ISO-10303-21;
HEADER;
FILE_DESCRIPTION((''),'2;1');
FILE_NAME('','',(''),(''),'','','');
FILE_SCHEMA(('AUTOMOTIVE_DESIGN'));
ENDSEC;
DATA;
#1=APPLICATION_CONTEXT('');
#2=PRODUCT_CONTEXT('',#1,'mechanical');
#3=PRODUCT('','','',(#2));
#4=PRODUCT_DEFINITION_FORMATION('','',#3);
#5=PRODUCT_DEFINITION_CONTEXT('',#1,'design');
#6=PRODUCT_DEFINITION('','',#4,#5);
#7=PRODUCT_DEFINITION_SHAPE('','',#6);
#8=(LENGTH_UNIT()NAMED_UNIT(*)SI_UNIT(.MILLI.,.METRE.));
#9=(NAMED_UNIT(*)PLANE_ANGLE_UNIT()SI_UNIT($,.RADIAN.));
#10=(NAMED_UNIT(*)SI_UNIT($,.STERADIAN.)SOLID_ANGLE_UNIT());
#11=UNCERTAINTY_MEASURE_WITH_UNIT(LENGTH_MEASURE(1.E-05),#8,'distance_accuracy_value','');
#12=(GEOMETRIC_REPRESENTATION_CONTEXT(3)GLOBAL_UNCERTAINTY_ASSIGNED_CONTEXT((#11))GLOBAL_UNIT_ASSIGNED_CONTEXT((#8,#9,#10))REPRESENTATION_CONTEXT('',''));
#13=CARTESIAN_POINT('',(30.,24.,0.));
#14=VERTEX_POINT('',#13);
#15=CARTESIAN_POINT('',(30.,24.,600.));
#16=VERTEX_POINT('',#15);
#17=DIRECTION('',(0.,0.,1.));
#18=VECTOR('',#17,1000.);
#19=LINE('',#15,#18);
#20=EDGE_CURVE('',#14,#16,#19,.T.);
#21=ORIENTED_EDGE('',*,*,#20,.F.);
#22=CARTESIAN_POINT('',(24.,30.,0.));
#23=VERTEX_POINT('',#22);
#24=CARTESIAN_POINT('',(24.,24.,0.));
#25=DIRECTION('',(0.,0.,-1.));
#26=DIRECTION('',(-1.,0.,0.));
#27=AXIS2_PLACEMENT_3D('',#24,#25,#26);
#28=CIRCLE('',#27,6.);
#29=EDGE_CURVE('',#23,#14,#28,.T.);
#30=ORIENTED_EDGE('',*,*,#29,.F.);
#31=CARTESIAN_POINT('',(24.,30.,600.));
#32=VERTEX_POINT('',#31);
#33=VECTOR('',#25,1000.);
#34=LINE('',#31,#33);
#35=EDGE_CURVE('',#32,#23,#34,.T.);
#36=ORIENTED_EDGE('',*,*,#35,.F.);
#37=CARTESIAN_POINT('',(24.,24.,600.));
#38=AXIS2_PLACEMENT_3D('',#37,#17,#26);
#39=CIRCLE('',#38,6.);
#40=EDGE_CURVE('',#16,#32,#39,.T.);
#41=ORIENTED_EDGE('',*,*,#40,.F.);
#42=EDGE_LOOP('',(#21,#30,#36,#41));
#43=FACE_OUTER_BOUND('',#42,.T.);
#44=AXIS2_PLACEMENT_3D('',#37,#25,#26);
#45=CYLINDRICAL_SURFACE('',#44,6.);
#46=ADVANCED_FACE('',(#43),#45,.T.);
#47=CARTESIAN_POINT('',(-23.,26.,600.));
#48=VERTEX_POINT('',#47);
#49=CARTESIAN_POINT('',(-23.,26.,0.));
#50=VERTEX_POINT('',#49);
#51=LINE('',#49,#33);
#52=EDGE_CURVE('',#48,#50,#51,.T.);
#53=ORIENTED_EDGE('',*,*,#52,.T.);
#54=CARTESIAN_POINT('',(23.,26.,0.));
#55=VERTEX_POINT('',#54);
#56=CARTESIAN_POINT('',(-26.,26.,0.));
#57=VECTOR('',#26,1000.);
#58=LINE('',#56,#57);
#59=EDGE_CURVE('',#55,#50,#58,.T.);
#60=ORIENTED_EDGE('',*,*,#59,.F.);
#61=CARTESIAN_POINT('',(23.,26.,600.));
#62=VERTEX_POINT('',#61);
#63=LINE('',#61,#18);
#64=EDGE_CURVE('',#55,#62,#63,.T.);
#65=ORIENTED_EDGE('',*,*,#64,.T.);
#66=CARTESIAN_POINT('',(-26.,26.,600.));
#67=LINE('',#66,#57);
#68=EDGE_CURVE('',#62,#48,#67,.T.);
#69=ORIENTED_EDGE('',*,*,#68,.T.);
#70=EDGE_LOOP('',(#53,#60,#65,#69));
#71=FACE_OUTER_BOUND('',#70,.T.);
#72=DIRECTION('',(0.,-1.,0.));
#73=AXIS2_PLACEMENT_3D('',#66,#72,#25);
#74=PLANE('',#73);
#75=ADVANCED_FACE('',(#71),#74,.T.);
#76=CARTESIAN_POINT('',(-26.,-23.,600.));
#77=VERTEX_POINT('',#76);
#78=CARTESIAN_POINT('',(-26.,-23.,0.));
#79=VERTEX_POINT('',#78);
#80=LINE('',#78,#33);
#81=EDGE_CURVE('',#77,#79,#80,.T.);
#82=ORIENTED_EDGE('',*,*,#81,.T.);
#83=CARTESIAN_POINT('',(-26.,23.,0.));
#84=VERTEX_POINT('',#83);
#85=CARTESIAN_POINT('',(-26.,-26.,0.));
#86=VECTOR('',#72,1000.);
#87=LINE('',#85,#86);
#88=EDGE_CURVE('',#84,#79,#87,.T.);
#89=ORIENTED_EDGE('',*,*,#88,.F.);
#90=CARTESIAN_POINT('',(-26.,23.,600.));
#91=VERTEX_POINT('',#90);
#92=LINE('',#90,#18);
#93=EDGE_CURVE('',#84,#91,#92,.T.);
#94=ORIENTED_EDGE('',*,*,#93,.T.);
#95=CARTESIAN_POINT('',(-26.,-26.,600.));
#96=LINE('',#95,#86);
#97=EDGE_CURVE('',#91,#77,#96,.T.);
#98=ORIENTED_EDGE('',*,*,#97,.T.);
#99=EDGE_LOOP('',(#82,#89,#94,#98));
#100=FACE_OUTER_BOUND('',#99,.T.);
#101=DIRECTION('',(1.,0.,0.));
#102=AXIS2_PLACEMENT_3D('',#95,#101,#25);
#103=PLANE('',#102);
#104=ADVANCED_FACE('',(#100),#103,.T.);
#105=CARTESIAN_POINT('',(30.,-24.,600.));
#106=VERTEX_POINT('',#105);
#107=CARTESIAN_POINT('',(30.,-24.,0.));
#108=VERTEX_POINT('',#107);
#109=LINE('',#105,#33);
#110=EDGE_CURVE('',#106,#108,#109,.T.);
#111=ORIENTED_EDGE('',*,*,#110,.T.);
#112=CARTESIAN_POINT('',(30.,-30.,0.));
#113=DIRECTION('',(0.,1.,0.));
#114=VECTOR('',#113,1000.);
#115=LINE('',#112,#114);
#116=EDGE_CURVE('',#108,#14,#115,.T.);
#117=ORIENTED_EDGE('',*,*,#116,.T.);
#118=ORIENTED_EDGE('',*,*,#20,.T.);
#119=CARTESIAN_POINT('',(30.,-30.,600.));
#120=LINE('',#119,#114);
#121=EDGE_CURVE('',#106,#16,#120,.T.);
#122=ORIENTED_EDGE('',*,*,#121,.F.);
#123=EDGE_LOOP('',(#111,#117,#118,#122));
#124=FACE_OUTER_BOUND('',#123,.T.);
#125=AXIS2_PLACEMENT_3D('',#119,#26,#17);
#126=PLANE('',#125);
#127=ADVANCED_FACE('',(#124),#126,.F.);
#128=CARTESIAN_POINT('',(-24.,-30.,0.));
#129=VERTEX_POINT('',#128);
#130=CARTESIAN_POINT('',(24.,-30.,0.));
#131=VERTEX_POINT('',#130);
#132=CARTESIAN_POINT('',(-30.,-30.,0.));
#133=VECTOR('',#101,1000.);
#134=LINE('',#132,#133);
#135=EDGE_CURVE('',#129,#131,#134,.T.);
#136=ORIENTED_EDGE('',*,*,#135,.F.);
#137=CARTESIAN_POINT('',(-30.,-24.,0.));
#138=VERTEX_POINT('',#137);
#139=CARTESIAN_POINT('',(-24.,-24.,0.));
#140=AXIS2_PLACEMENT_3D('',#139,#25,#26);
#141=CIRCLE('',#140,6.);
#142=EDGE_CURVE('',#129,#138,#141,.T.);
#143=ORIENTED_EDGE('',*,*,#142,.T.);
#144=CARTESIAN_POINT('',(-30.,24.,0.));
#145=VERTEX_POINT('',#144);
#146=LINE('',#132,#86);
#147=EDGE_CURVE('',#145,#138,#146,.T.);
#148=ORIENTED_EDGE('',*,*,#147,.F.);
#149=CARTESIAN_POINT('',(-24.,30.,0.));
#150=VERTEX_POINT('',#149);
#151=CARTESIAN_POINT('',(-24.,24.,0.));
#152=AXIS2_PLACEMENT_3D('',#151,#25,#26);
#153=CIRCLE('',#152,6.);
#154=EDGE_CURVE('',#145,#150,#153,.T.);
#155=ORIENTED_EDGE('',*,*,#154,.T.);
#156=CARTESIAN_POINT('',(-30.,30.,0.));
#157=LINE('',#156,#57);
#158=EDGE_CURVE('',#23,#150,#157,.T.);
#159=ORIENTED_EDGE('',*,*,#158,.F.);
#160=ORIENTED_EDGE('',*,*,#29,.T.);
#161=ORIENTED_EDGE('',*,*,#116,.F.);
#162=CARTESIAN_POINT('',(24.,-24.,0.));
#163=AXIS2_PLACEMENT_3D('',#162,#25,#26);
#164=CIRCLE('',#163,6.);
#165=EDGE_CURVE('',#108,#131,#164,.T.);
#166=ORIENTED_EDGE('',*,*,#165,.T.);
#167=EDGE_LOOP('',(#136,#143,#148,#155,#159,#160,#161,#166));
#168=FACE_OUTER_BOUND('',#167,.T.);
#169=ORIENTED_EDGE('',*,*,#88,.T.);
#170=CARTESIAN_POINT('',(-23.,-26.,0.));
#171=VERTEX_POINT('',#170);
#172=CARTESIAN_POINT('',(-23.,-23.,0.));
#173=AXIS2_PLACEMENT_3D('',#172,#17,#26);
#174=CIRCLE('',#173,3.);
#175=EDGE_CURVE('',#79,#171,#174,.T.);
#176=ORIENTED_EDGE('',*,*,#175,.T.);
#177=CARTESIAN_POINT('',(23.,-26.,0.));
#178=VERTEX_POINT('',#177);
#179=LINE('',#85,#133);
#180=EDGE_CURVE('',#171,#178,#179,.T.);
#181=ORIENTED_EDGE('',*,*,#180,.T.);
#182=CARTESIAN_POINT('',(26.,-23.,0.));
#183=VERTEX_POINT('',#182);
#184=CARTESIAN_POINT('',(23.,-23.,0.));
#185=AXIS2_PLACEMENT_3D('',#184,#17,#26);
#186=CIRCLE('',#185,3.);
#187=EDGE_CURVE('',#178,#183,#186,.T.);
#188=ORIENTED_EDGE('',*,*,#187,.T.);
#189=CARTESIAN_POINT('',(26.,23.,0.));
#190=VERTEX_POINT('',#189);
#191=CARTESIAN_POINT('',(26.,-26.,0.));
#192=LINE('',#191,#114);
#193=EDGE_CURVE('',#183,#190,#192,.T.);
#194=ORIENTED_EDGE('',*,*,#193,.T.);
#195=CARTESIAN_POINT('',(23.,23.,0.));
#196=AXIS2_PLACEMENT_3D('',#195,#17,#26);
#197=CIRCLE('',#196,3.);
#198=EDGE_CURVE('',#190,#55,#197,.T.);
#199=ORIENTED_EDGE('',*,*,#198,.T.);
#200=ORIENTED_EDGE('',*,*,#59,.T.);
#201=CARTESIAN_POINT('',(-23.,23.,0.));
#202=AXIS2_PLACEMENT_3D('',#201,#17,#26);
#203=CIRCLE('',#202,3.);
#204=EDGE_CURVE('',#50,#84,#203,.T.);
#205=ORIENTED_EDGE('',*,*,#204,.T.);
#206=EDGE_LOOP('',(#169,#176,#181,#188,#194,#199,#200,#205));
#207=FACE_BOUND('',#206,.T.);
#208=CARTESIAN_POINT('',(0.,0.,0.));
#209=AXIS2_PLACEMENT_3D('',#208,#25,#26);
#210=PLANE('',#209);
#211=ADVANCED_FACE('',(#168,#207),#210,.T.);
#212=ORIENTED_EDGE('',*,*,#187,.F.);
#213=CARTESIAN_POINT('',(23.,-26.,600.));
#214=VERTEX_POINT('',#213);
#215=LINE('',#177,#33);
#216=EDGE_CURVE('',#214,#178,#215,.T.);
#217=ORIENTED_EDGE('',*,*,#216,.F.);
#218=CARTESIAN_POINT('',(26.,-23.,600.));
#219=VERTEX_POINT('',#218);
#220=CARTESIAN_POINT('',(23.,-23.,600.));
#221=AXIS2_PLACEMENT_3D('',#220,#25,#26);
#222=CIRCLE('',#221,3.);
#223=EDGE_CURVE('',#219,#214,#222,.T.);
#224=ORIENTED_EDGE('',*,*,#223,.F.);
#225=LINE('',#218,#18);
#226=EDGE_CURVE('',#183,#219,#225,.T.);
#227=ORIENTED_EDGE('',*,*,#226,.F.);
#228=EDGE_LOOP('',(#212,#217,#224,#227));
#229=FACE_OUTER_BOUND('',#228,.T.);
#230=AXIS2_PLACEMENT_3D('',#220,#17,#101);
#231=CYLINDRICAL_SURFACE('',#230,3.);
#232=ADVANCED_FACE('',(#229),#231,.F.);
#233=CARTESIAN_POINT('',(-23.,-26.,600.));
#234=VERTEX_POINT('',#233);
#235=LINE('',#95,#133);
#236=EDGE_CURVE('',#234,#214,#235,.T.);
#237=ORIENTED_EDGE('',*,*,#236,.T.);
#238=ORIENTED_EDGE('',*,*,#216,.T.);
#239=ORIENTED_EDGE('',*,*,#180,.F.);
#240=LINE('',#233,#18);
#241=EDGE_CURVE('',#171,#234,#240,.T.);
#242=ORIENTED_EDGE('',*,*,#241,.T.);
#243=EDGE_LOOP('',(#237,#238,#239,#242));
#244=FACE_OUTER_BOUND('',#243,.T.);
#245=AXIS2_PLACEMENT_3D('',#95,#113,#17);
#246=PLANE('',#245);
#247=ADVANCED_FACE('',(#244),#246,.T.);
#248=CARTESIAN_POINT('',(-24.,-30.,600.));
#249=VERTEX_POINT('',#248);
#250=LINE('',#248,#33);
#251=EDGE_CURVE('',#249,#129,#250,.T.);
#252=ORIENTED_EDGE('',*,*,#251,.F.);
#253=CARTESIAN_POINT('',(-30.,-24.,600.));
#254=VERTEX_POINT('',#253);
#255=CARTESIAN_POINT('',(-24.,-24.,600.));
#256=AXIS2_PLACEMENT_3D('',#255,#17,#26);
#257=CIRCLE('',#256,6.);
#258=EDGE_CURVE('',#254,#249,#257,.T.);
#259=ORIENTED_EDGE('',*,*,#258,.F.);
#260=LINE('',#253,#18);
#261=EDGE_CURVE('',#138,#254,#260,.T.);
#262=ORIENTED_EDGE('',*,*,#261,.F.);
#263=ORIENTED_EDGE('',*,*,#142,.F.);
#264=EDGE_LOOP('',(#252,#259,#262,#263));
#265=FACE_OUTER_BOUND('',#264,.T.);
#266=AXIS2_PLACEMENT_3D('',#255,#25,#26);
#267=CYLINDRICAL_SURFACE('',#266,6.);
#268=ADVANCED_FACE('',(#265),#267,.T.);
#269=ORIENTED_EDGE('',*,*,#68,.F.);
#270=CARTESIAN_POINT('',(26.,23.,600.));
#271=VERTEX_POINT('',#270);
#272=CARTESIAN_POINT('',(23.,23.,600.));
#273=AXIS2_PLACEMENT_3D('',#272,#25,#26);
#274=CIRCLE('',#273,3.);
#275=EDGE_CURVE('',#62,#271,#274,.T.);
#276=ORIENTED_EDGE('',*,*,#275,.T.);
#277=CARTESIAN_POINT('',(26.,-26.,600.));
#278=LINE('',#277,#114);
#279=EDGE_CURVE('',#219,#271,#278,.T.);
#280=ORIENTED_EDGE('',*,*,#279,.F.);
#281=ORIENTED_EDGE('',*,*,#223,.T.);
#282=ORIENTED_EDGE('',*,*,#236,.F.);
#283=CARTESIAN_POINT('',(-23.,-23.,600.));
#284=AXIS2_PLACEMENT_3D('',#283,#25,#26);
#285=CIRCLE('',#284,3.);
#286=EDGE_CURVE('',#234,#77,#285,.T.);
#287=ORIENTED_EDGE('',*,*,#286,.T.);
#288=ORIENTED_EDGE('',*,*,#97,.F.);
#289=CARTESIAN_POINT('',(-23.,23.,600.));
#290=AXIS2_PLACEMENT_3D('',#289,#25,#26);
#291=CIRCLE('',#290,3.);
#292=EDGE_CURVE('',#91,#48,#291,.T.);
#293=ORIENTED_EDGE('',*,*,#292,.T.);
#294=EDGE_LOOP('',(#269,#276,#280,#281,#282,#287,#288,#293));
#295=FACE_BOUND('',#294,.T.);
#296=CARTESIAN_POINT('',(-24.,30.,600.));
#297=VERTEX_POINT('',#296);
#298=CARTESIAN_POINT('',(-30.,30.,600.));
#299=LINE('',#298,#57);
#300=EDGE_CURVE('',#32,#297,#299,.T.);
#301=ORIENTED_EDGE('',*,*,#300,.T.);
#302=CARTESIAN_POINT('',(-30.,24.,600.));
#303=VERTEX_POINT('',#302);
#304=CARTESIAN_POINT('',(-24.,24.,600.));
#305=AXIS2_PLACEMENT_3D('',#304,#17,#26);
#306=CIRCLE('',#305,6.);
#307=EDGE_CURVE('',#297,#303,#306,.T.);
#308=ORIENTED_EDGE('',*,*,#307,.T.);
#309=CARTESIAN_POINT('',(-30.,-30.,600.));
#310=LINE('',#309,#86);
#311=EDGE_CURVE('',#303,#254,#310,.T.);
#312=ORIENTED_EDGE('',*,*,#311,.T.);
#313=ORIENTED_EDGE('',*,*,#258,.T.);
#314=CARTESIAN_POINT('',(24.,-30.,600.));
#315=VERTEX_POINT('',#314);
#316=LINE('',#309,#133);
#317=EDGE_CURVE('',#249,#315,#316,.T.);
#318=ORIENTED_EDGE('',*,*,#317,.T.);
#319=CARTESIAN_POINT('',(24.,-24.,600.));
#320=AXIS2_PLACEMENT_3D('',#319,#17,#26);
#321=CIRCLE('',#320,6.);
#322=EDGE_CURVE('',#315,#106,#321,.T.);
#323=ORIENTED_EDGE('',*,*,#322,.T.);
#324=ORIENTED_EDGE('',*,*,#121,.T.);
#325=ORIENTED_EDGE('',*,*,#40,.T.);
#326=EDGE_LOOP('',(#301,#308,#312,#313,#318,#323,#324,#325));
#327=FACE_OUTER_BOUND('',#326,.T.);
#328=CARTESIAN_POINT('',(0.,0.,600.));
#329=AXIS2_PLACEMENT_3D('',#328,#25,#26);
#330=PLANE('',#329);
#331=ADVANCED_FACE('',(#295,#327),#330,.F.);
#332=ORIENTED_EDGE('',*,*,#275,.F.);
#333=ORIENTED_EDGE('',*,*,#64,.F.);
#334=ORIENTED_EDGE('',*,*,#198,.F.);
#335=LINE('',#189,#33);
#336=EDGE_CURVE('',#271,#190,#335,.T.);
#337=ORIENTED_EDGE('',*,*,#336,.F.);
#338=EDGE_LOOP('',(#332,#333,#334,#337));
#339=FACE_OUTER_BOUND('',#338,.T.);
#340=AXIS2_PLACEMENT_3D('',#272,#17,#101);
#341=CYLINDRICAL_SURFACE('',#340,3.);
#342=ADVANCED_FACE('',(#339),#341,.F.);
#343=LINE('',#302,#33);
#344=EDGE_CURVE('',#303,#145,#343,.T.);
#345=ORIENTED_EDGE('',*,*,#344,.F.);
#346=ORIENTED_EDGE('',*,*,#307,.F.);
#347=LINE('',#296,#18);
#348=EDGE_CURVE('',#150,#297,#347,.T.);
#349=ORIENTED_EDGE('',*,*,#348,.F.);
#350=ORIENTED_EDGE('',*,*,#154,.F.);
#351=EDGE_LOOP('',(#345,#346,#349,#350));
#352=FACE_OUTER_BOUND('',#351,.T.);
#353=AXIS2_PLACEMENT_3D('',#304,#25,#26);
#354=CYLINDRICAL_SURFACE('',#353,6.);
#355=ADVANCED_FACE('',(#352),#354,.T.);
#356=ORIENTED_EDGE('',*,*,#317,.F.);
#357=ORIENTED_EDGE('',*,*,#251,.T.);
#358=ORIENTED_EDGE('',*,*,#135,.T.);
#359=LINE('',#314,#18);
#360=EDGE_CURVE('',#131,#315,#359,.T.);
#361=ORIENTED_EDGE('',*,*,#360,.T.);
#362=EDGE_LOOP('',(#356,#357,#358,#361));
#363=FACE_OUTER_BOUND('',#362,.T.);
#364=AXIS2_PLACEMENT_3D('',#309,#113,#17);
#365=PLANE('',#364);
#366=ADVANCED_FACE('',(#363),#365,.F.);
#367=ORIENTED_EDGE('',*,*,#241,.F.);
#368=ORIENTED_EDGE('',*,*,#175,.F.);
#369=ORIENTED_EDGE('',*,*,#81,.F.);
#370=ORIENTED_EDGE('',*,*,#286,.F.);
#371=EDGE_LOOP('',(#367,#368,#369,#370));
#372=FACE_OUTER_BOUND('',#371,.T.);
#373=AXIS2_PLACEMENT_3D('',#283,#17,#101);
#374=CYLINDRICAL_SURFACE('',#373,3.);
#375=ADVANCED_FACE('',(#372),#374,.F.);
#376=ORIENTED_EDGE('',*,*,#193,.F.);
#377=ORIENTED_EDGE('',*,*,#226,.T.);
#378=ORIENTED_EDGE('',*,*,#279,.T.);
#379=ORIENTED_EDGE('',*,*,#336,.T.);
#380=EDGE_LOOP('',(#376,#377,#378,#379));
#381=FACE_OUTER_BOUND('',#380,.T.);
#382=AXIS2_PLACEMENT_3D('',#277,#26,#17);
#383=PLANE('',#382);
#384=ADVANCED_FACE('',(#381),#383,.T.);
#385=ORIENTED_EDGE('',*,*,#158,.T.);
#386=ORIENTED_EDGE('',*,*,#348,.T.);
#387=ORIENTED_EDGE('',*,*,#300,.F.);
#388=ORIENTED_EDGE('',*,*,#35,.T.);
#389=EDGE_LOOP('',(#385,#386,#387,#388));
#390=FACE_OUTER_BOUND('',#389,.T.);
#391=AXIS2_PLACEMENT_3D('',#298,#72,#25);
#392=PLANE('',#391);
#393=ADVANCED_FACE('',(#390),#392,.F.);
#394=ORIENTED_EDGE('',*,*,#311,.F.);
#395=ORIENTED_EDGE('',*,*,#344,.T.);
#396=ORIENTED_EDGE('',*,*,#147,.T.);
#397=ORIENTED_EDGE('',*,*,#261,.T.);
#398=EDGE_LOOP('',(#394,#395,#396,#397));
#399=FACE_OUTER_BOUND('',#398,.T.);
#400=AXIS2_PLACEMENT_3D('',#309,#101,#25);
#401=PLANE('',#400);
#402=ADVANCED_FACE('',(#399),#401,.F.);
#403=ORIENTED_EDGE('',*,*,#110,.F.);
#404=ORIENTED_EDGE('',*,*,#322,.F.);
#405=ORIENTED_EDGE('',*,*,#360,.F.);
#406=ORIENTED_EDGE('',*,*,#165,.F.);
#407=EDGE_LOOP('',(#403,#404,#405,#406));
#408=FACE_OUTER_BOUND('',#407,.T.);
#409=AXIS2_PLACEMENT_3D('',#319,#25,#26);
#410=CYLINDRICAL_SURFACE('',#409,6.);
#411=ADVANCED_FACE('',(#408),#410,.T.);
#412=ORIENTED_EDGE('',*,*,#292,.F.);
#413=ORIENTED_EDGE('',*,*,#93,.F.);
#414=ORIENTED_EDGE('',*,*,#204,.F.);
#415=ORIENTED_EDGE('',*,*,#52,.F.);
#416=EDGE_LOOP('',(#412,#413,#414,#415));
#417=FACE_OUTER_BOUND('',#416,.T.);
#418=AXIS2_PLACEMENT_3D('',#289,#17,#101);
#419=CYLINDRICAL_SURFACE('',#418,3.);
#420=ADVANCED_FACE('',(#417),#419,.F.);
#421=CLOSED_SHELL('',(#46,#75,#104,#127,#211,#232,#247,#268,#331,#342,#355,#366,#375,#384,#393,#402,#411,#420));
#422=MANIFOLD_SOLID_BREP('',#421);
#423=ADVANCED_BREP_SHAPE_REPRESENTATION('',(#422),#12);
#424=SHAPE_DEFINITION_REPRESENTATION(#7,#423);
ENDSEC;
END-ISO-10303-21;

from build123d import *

# Parameters (mm, degrees)
SKETCH1_W           = 60
SKETCH1_H           = 60
SKETCH1_W_2         = 52
SKETCH1_H_2         = 52
BOSS_EXTRUDE1_DEPTH = 600
FILLET1_R           = 6
FILLET2_R           = 3


with BuildPart() as part:
    # Sketch1 → Boss-Extrude1 (new body)
    with BuildSketch(Plane.XY):
        Rectangle(SKETCH1_W, SKETCH1_H)
        Rectangle(SKETCH1_W_2, SKETCH1_H_2, mode=Mode.SUBTRACT)
    extrude(amount=BOSS_EXTRUDE1_DEPTH)

    # Fillet1
    fillet1_edges = [part.edges().sort_by_distance(p)[0] for p in [
        (30, -30, 300),
        (-30, -30, 300),
        (-30, 30, 300),
        (30, 30, 300),
    ]]
    fillet(fillet1_edges, radius=FILLET1_R)

    # Fillet2
    fillet2_edges = [part.edges().sort_by_distance(p)[0] for p in [
        (26, -26, 300),
        (26, 26, 300),
        (-26, 26, 300),
        (-26, -26, 300),
    ]]
    fillet(fillet2_edges, radius=FILLET2_R)


solid = part.part
